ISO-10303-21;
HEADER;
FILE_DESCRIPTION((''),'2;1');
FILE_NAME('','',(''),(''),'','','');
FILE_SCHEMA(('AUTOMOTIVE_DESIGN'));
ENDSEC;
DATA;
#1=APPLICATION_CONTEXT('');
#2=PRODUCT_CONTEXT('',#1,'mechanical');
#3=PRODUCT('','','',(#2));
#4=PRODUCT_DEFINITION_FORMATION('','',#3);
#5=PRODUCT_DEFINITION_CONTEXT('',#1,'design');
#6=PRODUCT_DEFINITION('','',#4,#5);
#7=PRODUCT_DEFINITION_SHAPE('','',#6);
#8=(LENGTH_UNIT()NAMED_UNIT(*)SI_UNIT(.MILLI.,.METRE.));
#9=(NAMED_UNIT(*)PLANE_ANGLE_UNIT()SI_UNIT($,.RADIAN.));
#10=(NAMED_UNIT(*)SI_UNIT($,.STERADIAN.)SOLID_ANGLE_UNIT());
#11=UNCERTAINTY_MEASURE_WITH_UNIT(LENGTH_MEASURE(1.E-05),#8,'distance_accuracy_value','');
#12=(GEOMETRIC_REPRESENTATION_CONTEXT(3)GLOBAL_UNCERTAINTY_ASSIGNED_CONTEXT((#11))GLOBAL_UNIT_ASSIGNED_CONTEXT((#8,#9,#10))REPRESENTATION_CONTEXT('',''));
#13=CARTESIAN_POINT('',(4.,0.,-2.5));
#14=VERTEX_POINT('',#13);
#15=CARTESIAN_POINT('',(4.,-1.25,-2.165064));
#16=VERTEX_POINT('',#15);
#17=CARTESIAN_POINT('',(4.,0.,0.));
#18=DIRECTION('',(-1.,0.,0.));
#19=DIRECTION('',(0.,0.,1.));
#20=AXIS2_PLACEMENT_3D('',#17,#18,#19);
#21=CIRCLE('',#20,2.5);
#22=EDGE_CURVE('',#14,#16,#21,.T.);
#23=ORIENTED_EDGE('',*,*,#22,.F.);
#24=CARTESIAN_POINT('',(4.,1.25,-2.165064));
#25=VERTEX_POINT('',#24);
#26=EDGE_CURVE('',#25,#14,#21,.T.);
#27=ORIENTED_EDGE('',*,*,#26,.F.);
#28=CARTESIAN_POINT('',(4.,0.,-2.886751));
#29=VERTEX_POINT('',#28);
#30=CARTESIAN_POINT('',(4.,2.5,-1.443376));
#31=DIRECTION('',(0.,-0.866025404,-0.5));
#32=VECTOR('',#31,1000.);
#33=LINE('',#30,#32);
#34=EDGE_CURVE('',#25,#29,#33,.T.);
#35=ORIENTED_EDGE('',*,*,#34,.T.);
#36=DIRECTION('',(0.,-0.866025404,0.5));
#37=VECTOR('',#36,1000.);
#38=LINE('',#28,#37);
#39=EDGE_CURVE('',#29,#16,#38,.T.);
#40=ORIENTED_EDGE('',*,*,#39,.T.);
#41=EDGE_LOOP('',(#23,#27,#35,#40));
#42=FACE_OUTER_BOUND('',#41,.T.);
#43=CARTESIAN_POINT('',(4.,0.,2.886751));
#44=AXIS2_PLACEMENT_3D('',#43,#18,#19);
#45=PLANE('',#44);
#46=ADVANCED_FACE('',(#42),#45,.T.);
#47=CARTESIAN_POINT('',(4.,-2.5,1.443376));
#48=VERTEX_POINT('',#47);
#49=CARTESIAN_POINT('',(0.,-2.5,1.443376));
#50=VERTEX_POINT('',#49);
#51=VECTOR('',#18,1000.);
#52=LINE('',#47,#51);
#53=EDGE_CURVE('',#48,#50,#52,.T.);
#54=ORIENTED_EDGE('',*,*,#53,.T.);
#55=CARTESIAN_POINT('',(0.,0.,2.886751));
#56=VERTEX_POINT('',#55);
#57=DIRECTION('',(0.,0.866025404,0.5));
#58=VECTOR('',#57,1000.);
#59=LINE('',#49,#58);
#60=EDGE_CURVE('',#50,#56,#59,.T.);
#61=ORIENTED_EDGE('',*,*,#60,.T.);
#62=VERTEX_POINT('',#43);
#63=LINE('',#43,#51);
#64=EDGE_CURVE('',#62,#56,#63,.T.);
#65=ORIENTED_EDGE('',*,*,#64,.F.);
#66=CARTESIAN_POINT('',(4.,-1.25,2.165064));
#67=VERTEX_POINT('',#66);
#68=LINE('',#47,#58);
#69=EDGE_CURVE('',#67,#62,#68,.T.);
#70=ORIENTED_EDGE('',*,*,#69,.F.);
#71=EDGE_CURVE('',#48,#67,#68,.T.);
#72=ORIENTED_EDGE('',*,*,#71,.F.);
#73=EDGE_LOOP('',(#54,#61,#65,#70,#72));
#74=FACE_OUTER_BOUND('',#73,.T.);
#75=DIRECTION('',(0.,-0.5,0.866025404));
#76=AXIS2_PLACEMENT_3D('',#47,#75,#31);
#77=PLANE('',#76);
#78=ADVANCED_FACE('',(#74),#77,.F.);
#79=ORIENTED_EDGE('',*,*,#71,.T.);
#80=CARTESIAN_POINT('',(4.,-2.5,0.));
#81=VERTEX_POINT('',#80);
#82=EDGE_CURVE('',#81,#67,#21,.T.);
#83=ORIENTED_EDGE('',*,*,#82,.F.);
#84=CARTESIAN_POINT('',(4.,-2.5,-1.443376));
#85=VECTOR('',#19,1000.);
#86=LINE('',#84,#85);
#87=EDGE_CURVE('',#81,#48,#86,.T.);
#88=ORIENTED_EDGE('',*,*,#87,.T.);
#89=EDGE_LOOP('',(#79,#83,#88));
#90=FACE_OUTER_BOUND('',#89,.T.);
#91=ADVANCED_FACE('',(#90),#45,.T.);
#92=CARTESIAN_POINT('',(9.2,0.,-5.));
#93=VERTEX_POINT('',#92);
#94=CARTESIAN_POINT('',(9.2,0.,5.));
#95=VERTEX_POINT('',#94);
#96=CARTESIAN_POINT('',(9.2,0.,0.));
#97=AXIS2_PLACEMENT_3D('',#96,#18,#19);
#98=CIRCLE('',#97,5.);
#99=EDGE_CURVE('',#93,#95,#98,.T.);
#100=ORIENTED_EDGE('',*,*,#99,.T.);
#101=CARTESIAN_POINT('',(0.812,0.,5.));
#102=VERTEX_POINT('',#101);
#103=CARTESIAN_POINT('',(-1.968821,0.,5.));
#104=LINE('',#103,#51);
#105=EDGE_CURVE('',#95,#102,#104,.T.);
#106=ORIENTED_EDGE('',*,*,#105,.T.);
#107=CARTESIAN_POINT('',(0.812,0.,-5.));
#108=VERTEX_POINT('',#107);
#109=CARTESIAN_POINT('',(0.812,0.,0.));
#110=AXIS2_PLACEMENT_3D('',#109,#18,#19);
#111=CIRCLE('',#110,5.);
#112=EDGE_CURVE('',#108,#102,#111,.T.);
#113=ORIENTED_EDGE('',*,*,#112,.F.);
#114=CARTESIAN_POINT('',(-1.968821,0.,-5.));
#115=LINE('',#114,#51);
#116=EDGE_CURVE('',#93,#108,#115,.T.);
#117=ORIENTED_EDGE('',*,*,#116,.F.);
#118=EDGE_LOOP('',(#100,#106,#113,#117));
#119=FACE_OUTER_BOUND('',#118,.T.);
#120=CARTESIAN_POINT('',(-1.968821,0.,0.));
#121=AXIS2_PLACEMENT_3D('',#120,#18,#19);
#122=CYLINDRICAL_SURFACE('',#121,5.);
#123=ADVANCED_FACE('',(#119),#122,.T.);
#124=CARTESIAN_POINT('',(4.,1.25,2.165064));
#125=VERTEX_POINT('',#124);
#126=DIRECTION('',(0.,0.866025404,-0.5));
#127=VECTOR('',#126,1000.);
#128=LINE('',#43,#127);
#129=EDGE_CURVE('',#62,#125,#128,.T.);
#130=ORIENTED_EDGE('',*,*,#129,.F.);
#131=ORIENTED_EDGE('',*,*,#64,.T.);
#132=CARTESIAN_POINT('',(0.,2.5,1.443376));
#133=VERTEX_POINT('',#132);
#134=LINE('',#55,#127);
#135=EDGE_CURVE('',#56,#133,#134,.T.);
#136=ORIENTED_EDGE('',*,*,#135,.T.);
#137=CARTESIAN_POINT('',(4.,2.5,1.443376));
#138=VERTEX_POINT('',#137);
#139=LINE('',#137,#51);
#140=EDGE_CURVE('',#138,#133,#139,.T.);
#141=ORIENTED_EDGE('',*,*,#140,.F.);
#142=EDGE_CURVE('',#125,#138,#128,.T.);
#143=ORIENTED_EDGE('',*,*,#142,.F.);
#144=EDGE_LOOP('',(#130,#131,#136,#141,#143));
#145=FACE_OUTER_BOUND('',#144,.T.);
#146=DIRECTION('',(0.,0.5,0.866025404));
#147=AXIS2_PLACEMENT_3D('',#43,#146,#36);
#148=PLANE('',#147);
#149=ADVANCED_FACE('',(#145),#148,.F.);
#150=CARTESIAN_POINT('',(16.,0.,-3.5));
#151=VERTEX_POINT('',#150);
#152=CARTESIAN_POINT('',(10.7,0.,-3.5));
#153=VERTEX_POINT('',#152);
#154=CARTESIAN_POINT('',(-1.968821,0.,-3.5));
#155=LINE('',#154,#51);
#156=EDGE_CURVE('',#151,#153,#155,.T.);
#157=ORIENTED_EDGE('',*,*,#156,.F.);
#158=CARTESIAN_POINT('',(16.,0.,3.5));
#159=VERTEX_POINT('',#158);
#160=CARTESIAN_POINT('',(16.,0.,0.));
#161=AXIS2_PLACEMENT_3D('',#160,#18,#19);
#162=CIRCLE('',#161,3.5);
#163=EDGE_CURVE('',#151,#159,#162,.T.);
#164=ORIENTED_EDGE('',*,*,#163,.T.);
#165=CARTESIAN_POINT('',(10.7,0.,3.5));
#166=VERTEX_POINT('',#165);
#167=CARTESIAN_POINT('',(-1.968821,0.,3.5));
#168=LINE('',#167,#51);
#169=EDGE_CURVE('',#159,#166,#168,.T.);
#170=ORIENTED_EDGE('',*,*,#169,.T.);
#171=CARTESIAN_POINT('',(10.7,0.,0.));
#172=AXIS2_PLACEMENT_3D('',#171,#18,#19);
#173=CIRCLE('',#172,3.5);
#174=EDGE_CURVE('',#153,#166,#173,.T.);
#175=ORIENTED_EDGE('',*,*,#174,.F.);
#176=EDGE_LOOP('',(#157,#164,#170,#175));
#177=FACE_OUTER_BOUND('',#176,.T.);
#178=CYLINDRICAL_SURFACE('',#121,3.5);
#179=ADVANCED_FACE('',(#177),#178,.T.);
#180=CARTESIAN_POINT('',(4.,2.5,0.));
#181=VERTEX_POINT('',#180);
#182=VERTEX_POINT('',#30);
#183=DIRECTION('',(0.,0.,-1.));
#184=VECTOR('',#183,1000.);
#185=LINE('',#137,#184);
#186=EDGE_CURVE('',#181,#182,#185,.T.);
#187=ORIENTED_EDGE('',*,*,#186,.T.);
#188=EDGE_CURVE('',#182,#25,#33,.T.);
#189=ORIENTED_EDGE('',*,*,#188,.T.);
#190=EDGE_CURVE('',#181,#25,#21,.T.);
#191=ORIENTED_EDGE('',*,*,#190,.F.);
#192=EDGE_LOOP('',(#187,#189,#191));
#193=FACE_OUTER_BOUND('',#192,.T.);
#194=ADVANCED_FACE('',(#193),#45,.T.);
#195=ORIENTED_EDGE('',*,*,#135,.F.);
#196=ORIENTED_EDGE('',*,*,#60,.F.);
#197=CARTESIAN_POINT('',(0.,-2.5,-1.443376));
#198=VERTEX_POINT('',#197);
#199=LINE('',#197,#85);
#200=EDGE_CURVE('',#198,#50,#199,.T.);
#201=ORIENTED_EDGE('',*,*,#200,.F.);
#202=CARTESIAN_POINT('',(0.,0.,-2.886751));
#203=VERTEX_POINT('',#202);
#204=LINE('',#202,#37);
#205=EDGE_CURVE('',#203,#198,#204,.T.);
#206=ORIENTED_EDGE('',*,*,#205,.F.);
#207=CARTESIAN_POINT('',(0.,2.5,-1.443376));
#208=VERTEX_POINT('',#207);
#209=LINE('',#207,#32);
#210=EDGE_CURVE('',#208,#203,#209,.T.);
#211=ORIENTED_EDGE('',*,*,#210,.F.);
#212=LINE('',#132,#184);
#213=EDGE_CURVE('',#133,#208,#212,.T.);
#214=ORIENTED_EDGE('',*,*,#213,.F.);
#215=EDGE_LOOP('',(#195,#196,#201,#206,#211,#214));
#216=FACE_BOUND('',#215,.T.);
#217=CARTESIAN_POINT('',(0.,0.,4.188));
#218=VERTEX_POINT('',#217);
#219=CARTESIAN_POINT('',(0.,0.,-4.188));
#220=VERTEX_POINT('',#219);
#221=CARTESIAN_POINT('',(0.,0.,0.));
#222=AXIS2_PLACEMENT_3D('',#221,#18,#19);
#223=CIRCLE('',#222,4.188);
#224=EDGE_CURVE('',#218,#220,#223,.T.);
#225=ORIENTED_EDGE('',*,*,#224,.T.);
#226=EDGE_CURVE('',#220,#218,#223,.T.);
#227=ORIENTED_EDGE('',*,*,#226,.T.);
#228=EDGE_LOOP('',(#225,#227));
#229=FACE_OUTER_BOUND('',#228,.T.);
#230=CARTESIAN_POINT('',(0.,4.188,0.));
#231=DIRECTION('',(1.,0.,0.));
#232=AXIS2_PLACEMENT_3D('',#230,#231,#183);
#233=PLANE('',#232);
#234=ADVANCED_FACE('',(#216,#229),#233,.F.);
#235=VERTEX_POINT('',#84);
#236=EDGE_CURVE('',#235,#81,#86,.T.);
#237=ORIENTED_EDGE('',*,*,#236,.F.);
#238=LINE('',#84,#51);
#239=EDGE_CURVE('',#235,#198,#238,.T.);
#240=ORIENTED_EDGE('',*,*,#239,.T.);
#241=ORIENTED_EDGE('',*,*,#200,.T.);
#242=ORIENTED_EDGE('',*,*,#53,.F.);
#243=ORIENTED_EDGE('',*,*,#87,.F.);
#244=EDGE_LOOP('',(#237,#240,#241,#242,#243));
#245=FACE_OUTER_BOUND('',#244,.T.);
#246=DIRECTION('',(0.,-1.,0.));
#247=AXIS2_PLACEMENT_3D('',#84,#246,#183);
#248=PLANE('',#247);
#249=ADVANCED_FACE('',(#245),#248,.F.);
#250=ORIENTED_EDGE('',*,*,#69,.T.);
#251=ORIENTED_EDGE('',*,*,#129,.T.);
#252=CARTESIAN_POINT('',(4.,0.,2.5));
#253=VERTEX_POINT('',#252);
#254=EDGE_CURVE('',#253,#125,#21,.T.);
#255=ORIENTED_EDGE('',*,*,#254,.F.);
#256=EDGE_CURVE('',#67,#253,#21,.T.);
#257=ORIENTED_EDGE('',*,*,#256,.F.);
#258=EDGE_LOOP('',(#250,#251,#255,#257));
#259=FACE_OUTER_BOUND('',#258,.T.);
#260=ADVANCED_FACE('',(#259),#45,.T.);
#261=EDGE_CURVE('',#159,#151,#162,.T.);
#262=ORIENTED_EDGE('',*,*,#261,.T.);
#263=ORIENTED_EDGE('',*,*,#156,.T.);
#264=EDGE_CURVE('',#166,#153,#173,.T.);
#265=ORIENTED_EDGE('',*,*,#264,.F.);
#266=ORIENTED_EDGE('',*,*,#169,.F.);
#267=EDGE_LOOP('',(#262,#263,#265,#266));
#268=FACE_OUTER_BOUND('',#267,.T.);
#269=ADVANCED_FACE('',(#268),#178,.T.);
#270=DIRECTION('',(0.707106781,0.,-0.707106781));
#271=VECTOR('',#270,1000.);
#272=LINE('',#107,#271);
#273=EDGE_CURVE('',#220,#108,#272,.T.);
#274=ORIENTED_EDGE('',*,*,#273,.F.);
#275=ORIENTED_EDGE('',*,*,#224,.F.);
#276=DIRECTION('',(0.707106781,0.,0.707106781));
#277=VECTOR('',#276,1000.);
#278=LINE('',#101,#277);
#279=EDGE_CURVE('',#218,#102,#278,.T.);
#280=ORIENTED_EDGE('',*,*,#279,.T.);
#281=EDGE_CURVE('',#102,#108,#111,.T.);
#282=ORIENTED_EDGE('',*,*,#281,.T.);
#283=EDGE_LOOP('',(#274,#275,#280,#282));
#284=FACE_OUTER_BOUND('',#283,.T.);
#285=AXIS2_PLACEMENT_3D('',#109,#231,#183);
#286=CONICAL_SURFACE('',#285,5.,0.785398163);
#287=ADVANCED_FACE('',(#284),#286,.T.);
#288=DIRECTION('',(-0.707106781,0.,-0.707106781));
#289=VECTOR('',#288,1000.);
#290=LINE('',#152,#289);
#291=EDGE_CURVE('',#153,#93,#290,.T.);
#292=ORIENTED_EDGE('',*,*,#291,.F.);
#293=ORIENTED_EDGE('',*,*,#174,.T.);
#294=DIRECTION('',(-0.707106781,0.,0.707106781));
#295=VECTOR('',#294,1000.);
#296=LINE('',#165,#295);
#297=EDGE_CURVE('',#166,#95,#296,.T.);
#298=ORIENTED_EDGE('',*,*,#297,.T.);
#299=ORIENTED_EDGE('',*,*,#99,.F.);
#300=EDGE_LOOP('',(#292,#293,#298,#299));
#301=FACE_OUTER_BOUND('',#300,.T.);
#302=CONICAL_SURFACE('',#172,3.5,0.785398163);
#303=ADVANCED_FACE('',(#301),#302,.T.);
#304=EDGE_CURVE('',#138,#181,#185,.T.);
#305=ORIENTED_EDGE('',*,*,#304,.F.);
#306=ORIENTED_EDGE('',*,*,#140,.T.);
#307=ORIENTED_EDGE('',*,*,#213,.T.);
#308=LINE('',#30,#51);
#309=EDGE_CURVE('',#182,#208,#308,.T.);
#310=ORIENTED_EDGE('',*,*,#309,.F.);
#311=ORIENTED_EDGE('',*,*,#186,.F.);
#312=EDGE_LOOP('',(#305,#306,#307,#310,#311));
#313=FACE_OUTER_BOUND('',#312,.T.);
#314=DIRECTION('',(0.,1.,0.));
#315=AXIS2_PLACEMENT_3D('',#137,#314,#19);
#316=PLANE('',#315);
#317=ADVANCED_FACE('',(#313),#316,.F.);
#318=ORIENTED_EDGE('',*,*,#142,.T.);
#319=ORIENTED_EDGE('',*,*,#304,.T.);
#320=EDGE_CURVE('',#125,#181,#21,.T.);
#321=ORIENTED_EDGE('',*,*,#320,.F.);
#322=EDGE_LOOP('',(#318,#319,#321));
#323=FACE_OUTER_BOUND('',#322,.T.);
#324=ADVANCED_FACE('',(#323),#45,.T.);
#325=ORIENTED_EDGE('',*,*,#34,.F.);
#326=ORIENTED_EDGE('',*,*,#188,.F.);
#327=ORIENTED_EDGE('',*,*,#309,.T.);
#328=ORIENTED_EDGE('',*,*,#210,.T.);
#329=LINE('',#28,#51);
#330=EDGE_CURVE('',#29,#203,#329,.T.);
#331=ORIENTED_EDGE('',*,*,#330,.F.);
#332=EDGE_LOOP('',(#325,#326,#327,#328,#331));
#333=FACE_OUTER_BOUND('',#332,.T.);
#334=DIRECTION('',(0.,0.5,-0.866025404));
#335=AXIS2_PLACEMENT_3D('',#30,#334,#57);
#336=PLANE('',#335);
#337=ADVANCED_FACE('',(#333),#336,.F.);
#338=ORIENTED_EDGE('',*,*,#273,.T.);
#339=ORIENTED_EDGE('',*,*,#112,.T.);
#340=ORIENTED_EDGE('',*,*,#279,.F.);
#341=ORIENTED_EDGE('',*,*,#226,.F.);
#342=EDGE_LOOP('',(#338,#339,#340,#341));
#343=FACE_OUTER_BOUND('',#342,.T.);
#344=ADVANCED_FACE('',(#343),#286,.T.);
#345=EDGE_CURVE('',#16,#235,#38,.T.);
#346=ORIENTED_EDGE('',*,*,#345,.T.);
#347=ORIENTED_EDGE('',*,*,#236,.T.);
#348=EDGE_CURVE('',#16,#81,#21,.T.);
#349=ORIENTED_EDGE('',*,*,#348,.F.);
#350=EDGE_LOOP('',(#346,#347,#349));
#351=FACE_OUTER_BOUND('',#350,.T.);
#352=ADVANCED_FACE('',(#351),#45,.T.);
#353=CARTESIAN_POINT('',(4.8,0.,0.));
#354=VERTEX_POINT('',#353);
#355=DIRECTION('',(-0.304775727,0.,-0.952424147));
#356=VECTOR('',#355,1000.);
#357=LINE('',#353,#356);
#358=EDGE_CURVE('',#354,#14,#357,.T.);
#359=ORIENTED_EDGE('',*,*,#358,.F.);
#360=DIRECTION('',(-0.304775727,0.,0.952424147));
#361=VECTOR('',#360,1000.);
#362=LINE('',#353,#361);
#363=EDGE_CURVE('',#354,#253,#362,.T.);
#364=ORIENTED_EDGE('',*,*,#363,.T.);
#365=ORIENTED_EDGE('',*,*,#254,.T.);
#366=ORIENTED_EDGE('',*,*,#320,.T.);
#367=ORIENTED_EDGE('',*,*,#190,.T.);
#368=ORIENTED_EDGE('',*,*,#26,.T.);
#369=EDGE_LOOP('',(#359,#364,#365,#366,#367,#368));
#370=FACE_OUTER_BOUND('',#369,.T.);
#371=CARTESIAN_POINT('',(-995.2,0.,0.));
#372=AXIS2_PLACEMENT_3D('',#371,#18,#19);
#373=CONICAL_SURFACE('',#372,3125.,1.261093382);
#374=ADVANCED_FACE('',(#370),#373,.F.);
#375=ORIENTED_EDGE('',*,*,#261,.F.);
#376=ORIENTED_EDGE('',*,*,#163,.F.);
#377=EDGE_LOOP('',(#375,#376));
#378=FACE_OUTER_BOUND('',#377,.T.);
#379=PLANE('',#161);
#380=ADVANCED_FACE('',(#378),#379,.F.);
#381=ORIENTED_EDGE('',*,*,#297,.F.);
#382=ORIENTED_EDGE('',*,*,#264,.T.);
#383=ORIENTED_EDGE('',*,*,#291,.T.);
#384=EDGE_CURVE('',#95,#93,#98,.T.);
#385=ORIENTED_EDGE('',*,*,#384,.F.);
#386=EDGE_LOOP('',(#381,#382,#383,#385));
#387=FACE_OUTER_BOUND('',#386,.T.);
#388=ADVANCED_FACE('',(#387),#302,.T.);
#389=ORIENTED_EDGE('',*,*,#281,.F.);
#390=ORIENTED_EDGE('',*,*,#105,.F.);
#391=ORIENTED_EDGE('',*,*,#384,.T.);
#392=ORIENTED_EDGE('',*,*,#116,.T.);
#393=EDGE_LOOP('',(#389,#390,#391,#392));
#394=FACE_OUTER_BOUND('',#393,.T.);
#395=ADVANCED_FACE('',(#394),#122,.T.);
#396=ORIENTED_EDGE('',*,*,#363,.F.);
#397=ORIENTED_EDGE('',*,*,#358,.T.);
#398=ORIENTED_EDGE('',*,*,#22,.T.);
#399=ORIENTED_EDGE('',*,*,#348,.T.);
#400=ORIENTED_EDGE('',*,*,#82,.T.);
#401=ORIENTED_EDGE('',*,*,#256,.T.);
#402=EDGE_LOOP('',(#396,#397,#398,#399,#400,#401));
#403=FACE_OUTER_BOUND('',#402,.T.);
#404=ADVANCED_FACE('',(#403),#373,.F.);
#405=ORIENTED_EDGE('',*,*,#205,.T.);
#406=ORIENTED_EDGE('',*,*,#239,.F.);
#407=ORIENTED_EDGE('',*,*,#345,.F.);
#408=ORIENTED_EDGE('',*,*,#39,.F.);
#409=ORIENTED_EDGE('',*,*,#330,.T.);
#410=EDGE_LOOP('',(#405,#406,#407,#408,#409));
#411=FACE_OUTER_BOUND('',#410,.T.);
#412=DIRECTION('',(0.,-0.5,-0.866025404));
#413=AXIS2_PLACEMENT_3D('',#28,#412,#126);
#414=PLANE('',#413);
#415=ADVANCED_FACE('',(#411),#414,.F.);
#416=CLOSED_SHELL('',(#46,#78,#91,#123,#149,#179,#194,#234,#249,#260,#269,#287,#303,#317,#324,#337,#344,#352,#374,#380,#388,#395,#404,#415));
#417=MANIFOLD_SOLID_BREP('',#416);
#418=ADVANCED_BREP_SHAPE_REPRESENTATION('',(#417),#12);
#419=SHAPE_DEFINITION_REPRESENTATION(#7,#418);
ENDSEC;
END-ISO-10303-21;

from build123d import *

# Parameters (mm, degrees)
HEXAGONSOCKET_DEPTH = 4


with BuildPart() as part:
    # Sketch1 → Base (revolve)
    with BuildSketch(Plane.XY, mode=Mode.PRIVATE) as base_sk:
        Polygon((0, 0), (16, 0), (16, 3.5), (10.7, 3.5), (9.2, 5), (0.812, 5), (0, 4.188), align=None)
    revolve(base_sk.sketch.rotate(Axis((-1.968820569, 0, 0), (1, 0, 0)), 90), axis=Axis((-1.968820569, 0, 0), (1, 0, 0)))

    # Sketch2 → HexagonSocket (cut)
    with BuildSketch(Plane(origin=(0, -1.128463942, -0.35035393), x_dir=(0, 0, 1), z_dir=(-1, 0, 0))):
        Polygon((3.237105276, 1.128463942), (1.793729603, 3.628463942), (-1.093021743, 3.628463942), (-2.536397416, 1.128463942), (-1.093021743, -1.371536058), (1.793729603, -1.371536058), align=None)
    extrude(amount=-HEXAGONSOCKET_DEPTH, mode=Mode.SUBTRACT)

    # Sketch3 → Cut-Revolve1 (revolve, cut)
    with BuildSketch(Plane.XY, mode=Mode.PRIVATE) as cut_revolve1_sk:
        Polygon((4, 2.5), (4, 0), (4.8, 0), align=None)
    revolve(cut_revolve1_sk.sketch.rotate(Axis((-0.330994676, 0, 0), (1, 0, 0)), 90), axis=Axis((-0.330994676, 0, 0), (1, 0, 0)), mode=Mode.SUBTRACT)


solid = part.part
